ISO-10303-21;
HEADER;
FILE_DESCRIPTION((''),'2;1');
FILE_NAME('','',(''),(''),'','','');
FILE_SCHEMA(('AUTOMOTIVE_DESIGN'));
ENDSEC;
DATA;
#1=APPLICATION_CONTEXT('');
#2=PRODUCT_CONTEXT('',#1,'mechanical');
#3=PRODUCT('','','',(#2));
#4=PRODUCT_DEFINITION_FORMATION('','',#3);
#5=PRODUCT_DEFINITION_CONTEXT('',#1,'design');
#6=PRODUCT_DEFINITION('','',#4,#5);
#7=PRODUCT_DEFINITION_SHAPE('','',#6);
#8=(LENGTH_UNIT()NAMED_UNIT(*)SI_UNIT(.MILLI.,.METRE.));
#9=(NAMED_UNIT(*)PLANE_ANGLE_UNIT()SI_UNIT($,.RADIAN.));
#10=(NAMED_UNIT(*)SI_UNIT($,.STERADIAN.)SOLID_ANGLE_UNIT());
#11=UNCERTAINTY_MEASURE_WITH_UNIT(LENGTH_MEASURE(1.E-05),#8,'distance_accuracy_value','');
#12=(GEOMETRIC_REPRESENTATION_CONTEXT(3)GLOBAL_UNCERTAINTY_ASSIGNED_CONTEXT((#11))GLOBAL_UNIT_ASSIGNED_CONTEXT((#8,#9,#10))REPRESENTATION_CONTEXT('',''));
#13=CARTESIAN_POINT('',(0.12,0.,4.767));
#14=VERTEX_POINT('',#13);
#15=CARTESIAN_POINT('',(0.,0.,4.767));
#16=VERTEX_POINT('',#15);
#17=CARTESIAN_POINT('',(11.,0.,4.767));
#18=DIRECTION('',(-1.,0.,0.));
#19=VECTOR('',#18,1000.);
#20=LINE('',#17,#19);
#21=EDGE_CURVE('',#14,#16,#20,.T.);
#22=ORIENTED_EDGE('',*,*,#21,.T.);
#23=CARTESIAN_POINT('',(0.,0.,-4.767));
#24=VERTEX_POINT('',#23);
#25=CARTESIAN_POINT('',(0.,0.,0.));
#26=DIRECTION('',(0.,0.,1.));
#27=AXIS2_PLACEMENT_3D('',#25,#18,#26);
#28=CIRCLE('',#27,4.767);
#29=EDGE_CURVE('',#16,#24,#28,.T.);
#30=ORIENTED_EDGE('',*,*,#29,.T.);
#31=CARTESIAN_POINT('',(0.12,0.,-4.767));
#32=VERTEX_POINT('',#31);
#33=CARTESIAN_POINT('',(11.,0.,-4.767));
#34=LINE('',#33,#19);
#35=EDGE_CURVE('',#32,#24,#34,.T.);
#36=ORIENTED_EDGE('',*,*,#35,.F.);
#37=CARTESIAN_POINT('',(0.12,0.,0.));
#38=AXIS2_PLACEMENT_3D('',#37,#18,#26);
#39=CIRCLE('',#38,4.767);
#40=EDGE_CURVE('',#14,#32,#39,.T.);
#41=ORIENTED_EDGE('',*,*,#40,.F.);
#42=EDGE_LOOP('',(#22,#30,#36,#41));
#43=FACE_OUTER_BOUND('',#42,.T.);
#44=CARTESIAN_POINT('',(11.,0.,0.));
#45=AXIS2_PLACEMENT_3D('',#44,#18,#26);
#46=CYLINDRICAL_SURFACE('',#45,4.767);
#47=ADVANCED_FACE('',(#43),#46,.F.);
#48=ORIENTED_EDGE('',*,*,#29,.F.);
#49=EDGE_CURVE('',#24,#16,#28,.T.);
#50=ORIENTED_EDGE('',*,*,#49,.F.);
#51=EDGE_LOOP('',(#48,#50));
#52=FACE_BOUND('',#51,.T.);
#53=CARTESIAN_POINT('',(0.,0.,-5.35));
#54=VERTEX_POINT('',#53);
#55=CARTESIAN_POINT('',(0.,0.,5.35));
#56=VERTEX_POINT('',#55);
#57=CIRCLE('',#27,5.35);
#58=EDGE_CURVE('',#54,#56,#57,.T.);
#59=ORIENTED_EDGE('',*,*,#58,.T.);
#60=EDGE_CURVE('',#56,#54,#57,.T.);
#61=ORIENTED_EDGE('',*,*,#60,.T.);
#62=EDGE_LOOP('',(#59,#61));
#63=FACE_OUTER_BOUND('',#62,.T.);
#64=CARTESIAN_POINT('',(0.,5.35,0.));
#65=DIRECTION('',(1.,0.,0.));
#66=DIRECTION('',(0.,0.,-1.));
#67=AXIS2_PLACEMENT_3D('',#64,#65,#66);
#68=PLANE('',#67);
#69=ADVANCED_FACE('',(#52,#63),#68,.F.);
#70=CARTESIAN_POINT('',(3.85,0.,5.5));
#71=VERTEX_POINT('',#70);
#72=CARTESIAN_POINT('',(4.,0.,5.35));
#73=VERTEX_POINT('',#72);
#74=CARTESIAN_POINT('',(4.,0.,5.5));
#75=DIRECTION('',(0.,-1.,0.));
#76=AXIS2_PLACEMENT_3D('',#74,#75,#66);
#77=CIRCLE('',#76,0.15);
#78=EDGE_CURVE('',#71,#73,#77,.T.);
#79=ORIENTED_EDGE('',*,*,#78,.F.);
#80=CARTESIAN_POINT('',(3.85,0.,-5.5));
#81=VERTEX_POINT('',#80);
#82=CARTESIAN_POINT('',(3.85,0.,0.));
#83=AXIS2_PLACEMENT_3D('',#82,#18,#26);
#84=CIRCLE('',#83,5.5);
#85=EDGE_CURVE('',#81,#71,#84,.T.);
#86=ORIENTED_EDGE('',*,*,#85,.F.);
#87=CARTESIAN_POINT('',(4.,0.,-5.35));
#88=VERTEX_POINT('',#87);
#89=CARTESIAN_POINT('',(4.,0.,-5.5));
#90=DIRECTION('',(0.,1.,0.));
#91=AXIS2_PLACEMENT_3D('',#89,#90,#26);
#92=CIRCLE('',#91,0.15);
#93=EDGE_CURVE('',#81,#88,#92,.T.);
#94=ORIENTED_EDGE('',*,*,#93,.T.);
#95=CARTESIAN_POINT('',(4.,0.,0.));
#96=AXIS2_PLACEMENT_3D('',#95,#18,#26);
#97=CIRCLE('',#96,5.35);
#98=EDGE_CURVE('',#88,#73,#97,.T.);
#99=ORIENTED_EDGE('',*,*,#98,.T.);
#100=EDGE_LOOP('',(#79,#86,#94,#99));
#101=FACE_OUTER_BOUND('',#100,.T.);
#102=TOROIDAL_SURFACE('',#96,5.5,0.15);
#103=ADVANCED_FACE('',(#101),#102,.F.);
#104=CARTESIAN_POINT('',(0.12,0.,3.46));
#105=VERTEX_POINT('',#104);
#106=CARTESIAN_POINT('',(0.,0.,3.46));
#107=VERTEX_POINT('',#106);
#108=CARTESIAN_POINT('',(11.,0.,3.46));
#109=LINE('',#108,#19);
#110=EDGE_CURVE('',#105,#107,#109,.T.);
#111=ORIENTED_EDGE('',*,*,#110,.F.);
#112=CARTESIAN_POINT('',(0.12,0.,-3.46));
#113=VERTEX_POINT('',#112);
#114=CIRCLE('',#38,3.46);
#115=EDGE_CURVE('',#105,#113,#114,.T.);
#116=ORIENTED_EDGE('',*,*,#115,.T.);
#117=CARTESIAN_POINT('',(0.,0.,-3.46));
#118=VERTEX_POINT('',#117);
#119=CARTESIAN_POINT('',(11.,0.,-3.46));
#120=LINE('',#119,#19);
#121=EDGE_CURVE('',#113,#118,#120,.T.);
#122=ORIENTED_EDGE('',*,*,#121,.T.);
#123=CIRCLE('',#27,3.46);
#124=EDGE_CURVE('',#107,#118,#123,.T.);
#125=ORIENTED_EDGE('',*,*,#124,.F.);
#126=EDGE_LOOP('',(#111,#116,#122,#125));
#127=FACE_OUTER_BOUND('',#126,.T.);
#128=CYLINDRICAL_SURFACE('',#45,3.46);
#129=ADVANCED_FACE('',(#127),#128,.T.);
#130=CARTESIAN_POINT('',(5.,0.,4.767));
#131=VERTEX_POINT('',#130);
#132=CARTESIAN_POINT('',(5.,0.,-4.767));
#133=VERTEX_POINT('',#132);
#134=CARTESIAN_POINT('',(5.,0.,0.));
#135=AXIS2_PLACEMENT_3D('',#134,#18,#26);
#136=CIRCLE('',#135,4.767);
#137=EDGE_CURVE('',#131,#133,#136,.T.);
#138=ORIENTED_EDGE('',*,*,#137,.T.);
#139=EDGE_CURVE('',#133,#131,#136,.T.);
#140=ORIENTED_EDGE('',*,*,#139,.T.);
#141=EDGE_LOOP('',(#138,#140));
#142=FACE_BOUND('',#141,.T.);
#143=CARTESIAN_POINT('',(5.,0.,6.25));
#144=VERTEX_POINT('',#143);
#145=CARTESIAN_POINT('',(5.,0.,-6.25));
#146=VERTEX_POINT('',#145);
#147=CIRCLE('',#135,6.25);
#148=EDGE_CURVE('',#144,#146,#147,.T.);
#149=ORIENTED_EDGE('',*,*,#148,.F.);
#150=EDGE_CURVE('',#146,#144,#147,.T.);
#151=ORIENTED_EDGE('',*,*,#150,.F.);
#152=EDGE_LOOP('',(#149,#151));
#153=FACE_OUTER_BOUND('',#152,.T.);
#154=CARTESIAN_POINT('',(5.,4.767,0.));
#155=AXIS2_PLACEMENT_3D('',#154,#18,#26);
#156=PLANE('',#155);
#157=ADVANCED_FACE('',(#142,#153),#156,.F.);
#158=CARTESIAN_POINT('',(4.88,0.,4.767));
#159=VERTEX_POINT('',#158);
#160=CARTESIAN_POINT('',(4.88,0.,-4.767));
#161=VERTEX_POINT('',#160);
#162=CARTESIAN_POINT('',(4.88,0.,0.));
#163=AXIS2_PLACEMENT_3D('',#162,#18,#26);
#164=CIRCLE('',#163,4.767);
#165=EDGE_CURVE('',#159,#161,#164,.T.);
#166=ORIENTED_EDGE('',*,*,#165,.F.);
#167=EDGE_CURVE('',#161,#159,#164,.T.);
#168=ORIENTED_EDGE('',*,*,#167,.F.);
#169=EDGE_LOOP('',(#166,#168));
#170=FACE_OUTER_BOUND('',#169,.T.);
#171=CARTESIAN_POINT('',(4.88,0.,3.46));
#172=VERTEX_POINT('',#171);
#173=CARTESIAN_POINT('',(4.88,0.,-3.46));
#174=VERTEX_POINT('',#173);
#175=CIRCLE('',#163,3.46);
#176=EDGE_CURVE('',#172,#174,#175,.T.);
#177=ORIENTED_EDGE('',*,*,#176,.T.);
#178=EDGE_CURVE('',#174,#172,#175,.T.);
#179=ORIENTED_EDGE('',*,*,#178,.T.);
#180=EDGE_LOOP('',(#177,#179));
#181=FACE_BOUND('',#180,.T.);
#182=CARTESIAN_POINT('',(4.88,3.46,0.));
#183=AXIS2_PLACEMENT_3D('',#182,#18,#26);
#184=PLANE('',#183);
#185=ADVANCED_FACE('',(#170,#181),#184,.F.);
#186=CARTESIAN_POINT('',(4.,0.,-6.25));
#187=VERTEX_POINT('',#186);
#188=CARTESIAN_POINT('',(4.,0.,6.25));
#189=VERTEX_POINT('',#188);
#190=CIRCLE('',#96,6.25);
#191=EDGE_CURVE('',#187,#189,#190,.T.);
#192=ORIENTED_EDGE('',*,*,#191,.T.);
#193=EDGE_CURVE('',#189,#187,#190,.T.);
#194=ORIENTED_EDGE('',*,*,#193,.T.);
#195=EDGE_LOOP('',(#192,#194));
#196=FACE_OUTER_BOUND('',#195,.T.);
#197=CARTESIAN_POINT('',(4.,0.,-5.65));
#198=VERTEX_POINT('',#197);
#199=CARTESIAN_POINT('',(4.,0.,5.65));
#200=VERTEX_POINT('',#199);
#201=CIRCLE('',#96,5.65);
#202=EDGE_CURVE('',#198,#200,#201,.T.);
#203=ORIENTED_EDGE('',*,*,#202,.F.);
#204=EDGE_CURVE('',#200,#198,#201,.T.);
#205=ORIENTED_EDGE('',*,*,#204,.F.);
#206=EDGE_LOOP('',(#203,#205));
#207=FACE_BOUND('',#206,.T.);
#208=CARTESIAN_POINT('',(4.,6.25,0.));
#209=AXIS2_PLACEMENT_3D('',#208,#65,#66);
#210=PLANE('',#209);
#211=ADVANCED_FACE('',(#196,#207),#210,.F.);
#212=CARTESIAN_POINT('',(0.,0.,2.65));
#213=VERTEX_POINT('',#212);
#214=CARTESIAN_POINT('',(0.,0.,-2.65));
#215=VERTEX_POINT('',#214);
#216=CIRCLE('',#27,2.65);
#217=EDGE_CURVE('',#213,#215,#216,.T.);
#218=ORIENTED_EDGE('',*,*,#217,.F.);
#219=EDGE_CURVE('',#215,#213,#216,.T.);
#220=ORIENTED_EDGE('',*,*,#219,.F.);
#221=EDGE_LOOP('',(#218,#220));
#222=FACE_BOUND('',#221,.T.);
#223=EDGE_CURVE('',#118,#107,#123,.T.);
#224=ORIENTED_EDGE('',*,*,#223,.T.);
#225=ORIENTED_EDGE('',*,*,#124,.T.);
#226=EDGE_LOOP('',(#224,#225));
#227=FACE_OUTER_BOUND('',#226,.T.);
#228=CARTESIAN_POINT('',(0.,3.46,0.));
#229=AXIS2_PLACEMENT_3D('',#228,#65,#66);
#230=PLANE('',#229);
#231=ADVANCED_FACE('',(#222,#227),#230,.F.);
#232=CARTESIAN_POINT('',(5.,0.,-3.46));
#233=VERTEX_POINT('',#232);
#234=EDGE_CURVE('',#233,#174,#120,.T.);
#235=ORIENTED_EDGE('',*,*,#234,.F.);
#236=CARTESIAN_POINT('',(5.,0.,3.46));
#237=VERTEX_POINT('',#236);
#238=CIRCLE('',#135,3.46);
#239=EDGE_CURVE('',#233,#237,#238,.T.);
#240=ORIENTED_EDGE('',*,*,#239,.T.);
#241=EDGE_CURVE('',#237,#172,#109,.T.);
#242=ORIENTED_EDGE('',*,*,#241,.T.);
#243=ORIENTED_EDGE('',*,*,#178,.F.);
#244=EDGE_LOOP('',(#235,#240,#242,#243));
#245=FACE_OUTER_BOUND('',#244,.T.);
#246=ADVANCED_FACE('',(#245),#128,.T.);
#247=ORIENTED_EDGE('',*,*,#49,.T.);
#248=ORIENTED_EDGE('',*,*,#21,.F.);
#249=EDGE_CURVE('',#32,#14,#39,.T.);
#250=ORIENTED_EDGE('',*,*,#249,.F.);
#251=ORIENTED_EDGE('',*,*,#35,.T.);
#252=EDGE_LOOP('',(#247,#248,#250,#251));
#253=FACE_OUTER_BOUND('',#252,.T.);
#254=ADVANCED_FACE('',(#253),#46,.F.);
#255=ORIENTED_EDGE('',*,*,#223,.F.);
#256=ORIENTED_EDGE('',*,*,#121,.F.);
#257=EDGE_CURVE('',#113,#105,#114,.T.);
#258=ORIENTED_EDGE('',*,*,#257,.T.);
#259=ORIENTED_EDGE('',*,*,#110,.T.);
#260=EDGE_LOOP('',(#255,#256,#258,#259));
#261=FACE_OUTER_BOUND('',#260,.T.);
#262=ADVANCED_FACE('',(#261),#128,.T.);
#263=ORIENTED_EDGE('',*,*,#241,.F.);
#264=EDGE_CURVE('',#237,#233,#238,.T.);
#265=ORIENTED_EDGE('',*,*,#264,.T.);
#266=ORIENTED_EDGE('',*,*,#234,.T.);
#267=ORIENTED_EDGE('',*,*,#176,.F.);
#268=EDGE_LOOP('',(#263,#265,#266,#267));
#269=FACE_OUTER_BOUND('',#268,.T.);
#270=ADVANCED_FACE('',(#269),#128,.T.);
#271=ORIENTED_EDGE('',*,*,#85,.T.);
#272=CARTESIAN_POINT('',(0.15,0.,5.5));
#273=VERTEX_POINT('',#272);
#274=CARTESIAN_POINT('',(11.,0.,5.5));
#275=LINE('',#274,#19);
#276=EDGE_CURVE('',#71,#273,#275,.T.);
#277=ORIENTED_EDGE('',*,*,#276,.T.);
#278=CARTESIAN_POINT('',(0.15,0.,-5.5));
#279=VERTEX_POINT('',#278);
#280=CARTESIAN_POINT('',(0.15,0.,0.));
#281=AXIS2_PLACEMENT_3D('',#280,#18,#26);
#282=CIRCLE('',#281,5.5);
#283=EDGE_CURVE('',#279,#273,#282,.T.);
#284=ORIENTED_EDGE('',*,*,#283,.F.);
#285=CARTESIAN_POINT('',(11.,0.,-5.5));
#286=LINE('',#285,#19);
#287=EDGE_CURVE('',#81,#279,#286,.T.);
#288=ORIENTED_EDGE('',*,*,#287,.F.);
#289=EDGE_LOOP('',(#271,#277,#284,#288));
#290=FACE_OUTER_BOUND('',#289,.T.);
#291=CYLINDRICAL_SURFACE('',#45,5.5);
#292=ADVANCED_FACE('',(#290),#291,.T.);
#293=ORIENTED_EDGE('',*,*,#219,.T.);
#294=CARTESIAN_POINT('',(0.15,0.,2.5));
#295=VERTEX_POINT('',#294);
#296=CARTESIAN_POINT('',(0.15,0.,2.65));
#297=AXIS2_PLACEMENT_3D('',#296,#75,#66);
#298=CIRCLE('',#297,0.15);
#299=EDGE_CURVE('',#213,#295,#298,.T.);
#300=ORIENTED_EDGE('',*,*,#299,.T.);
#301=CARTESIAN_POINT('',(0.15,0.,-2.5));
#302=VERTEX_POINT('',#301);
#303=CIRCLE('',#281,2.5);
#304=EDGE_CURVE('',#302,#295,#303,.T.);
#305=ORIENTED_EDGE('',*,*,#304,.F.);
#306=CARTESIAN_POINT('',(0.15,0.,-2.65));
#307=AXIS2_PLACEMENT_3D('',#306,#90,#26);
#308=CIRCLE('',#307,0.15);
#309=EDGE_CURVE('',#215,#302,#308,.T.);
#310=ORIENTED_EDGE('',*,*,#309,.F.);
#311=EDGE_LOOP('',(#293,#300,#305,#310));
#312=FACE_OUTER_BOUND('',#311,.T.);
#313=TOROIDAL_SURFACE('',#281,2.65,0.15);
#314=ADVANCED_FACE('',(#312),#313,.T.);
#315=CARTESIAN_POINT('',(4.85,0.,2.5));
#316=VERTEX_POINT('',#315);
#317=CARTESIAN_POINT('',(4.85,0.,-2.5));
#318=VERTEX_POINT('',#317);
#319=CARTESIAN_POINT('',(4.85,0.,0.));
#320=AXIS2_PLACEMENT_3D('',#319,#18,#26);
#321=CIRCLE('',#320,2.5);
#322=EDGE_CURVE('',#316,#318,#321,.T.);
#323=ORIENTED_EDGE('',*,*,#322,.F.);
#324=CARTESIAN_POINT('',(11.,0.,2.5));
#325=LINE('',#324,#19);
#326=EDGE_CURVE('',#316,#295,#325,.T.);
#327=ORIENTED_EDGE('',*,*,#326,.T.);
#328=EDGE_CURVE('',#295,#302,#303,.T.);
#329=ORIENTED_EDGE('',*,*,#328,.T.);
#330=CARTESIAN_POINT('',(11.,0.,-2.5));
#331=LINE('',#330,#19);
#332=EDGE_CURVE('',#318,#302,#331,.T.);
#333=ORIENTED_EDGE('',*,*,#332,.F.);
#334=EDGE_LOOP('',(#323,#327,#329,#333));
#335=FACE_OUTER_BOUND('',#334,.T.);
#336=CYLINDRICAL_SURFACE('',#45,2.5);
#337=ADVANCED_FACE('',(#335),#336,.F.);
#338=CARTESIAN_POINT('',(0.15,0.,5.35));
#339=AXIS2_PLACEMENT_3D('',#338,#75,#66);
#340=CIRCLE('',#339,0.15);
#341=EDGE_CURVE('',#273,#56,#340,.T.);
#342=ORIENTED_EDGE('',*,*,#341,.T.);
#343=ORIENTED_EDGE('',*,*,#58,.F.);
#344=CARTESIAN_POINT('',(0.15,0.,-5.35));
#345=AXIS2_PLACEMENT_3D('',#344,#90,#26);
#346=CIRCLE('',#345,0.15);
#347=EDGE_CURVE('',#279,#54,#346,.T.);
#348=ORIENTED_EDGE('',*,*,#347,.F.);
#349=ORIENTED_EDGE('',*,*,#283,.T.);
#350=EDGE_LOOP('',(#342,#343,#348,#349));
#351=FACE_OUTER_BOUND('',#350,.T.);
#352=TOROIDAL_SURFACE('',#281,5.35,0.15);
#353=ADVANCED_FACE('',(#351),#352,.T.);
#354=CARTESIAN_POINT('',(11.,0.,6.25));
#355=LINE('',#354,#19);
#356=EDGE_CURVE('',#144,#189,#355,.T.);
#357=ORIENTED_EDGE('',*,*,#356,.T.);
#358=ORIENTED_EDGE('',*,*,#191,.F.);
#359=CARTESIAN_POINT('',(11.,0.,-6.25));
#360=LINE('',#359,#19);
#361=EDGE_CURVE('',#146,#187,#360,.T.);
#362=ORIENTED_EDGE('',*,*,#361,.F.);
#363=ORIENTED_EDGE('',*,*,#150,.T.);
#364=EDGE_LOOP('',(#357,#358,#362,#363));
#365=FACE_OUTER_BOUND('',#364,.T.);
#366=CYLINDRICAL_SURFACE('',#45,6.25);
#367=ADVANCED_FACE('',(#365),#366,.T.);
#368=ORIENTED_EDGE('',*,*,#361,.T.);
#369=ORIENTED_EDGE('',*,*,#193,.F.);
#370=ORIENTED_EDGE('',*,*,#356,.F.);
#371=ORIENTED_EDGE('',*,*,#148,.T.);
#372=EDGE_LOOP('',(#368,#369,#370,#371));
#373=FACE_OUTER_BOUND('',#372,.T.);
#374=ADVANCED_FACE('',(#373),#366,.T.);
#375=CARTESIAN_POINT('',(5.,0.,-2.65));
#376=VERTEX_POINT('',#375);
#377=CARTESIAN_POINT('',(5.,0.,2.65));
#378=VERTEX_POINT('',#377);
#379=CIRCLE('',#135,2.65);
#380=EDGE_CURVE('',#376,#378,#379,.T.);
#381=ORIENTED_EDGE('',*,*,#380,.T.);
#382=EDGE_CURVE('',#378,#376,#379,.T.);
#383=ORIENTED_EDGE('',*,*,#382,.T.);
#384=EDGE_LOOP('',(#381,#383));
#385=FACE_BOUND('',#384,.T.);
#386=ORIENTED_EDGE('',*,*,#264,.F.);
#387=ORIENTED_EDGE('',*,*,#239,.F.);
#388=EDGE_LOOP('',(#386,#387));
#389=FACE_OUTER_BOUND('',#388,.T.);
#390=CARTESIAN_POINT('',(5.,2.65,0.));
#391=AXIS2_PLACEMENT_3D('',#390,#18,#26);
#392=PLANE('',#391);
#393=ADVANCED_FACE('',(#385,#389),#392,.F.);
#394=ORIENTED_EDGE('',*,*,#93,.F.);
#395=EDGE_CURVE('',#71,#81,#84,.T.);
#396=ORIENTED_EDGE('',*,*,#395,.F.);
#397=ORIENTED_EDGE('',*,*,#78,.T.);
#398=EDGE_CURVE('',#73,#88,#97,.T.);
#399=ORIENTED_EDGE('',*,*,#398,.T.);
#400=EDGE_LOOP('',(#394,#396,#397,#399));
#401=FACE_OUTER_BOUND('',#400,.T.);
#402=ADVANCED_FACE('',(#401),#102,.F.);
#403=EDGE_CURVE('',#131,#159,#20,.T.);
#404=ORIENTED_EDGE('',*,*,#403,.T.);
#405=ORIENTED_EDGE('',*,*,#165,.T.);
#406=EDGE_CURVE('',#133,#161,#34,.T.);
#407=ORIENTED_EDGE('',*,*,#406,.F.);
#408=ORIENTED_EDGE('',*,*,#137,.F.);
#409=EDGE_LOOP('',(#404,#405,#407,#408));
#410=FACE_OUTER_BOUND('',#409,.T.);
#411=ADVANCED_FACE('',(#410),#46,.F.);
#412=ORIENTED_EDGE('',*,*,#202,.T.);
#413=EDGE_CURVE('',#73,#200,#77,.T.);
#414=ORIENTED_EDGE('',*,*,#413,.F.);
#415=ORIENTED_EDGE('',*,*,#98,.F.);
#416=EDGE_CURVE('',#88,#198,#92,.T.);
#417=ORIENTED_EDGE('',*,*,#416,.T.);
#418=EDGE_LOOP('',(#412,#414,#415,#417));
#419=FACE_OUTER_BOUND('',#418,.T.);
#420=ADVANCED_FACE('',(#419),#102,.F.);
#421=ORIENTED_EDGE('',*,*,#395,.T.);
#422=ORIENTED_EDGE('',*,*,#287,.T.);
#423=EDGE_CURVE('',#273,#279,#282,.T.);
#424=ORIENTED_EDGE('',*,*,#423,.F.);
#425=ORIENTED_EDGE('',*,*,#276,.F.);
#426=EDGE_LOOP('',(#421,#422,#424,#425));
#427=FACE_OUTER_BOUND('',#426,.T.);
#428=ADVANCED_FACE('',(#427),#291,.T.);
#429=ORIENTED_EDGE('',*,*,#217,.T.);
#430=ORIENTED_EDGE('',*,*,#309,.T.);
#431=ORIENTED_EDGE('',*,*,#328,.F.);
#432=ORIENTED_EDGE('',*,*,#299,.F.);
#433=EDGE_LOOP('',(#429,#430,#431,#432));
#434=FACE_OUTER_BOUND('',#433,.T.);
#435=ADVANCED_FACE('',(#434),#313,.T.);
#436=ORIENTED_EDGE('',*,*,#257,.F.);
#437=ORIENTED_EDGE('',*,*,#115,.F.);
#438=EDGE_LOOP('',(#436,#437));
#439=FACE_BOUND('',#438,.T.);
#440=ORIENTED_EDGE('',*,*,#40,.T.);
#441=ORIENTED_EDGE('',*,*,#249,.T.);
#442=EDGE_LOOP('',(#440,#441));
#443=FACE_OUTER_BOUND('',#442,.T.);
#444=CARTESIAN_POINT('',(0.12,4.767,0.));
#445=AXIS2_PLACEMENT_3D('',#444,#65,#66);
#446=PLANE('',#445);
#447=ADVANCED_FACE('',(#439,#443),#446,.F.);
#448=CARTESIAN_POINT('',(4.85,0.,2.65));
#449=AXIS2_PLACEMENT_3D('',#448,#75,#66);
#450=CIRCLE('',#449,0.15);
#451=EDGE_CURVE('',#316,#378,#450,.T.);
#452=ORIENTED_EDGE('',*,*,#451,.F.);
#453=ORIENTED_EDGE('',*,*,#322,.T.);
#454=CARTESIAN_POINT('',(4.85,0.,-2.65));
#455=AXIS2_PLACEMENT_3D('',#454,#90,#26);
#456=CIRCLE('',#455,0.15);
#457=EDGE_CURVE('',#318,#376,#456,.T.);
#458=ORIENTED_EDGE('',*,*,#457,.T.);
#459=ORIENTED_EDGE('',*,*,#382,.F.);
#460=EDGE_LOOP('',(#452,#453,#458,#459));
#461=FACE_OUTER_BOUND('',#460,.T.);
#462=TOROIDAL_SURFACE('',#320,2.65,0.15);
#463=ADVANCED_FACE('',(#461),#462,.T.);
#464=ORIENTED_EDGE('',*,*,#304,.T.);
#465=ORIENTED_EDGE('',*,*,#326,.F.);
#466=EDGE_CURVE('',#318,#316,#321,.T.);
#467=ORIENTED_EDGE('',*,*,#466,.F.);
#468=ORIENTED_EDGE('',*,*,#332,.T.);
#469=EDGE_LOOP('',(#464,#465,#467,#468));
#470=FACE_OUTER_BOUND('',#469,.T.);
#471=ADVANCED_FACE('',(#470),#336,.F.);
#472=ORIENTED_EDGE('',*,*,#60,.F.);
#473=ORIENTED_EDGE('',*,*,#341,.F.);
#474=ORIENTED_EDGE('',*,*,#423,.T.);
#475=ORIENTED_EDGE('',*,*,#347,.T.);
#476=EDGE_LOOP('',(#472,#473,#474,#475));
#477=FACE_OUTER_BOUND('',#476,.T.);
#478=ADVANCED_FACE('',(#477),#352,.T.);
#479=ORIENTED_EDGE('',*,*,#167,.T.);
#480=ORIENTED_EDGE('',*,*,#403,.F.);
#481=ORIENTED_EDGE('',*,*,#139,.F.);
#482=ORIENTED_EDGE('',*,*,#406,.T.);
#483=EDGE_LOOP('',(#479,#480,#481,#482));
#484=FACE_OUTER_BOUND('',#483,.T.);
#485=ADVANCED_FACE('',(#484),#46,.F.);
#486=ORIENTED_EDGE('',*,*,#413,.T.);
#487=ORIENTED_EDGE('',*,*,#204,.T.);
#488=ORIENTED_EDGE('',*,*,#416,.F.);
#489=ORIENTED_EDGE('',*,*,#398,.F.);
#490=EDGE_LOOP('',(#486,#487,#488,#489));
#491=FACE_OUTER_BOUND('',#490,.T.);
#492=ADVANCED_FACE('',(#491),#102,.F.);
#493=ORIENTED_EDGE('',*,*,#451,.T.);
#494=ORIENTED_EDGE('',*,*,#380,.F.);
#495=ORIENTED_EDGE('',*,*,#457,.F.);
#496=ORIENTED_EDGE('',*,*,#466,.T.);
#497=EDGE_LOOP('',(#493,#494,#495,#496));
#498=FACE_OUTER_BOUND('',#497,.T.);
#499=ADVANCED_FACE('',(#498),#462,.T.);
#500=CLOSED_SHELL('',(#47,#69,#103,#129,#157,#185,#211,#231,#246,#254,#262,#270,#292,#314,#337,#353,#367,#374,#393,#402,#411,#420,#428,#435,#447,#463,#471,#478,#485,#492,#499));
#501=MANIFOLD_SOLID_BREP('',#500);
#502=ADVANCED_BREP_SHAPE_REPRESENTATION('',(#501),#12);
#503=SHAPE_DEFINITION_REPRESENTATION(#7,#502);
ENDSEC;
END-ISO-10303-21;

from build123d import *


with BuildPart() as part:
    # Sketch1 → Revolve1 (revolve)
    with BuildSketch(Plane.XY, mode=Mode.PRIVATE) as revolve1_sk:
        with BuildLine():
            Line((0, 5.35), (0, 4.767))
            Line((0, 4.767), (0.12, 4.767))
            Line((0.12, 4.767), (0.12, 3.46))
            Line((0.12, 3.46), (0, 3.46))
            Line((0, 3.46), (0, 2.65))
            ThreePointArc((0, 2.65), (0.043933983, 2.543933983), (0.15, 2.5))
            Line((0.15, 2.5), (4.85, 2.5))
            ThreePointArc((4.85, 2.5), (4.956066017, 2.543933983), (5, 2.65))
            Line((5, 2.65), (5, 3.46))
            Line((5, 3.46), (4.88, 3.46))
            Line((4.88, 3.46), (4.88, 4.767))
            Line((4.88, 4.767), (5, 4.767))
            Line((5, 4.767), (5, 6.25))
            Line((5, 6.25), (4, 6.25))
            Line((4, 6.25), (4, 5.65))
            ThreePointArc((4, 5.65), (4.106066017, 5.393933983), (3.85, 5.5))
            Line((3.85, 5.5), (0.15, 5.5))
            ThreePointArc((0.15, 5.5), (0.043933983, 5.456066017), (0, 5.35))
        make_face()
    revolve(revolve1_sk.sketch.rotate(Axis((11, 0, 0), (-1, 0, 0)), 270), axis=Axis((11, 0, 0), (-1, 0, 0)))


solid = part.part
